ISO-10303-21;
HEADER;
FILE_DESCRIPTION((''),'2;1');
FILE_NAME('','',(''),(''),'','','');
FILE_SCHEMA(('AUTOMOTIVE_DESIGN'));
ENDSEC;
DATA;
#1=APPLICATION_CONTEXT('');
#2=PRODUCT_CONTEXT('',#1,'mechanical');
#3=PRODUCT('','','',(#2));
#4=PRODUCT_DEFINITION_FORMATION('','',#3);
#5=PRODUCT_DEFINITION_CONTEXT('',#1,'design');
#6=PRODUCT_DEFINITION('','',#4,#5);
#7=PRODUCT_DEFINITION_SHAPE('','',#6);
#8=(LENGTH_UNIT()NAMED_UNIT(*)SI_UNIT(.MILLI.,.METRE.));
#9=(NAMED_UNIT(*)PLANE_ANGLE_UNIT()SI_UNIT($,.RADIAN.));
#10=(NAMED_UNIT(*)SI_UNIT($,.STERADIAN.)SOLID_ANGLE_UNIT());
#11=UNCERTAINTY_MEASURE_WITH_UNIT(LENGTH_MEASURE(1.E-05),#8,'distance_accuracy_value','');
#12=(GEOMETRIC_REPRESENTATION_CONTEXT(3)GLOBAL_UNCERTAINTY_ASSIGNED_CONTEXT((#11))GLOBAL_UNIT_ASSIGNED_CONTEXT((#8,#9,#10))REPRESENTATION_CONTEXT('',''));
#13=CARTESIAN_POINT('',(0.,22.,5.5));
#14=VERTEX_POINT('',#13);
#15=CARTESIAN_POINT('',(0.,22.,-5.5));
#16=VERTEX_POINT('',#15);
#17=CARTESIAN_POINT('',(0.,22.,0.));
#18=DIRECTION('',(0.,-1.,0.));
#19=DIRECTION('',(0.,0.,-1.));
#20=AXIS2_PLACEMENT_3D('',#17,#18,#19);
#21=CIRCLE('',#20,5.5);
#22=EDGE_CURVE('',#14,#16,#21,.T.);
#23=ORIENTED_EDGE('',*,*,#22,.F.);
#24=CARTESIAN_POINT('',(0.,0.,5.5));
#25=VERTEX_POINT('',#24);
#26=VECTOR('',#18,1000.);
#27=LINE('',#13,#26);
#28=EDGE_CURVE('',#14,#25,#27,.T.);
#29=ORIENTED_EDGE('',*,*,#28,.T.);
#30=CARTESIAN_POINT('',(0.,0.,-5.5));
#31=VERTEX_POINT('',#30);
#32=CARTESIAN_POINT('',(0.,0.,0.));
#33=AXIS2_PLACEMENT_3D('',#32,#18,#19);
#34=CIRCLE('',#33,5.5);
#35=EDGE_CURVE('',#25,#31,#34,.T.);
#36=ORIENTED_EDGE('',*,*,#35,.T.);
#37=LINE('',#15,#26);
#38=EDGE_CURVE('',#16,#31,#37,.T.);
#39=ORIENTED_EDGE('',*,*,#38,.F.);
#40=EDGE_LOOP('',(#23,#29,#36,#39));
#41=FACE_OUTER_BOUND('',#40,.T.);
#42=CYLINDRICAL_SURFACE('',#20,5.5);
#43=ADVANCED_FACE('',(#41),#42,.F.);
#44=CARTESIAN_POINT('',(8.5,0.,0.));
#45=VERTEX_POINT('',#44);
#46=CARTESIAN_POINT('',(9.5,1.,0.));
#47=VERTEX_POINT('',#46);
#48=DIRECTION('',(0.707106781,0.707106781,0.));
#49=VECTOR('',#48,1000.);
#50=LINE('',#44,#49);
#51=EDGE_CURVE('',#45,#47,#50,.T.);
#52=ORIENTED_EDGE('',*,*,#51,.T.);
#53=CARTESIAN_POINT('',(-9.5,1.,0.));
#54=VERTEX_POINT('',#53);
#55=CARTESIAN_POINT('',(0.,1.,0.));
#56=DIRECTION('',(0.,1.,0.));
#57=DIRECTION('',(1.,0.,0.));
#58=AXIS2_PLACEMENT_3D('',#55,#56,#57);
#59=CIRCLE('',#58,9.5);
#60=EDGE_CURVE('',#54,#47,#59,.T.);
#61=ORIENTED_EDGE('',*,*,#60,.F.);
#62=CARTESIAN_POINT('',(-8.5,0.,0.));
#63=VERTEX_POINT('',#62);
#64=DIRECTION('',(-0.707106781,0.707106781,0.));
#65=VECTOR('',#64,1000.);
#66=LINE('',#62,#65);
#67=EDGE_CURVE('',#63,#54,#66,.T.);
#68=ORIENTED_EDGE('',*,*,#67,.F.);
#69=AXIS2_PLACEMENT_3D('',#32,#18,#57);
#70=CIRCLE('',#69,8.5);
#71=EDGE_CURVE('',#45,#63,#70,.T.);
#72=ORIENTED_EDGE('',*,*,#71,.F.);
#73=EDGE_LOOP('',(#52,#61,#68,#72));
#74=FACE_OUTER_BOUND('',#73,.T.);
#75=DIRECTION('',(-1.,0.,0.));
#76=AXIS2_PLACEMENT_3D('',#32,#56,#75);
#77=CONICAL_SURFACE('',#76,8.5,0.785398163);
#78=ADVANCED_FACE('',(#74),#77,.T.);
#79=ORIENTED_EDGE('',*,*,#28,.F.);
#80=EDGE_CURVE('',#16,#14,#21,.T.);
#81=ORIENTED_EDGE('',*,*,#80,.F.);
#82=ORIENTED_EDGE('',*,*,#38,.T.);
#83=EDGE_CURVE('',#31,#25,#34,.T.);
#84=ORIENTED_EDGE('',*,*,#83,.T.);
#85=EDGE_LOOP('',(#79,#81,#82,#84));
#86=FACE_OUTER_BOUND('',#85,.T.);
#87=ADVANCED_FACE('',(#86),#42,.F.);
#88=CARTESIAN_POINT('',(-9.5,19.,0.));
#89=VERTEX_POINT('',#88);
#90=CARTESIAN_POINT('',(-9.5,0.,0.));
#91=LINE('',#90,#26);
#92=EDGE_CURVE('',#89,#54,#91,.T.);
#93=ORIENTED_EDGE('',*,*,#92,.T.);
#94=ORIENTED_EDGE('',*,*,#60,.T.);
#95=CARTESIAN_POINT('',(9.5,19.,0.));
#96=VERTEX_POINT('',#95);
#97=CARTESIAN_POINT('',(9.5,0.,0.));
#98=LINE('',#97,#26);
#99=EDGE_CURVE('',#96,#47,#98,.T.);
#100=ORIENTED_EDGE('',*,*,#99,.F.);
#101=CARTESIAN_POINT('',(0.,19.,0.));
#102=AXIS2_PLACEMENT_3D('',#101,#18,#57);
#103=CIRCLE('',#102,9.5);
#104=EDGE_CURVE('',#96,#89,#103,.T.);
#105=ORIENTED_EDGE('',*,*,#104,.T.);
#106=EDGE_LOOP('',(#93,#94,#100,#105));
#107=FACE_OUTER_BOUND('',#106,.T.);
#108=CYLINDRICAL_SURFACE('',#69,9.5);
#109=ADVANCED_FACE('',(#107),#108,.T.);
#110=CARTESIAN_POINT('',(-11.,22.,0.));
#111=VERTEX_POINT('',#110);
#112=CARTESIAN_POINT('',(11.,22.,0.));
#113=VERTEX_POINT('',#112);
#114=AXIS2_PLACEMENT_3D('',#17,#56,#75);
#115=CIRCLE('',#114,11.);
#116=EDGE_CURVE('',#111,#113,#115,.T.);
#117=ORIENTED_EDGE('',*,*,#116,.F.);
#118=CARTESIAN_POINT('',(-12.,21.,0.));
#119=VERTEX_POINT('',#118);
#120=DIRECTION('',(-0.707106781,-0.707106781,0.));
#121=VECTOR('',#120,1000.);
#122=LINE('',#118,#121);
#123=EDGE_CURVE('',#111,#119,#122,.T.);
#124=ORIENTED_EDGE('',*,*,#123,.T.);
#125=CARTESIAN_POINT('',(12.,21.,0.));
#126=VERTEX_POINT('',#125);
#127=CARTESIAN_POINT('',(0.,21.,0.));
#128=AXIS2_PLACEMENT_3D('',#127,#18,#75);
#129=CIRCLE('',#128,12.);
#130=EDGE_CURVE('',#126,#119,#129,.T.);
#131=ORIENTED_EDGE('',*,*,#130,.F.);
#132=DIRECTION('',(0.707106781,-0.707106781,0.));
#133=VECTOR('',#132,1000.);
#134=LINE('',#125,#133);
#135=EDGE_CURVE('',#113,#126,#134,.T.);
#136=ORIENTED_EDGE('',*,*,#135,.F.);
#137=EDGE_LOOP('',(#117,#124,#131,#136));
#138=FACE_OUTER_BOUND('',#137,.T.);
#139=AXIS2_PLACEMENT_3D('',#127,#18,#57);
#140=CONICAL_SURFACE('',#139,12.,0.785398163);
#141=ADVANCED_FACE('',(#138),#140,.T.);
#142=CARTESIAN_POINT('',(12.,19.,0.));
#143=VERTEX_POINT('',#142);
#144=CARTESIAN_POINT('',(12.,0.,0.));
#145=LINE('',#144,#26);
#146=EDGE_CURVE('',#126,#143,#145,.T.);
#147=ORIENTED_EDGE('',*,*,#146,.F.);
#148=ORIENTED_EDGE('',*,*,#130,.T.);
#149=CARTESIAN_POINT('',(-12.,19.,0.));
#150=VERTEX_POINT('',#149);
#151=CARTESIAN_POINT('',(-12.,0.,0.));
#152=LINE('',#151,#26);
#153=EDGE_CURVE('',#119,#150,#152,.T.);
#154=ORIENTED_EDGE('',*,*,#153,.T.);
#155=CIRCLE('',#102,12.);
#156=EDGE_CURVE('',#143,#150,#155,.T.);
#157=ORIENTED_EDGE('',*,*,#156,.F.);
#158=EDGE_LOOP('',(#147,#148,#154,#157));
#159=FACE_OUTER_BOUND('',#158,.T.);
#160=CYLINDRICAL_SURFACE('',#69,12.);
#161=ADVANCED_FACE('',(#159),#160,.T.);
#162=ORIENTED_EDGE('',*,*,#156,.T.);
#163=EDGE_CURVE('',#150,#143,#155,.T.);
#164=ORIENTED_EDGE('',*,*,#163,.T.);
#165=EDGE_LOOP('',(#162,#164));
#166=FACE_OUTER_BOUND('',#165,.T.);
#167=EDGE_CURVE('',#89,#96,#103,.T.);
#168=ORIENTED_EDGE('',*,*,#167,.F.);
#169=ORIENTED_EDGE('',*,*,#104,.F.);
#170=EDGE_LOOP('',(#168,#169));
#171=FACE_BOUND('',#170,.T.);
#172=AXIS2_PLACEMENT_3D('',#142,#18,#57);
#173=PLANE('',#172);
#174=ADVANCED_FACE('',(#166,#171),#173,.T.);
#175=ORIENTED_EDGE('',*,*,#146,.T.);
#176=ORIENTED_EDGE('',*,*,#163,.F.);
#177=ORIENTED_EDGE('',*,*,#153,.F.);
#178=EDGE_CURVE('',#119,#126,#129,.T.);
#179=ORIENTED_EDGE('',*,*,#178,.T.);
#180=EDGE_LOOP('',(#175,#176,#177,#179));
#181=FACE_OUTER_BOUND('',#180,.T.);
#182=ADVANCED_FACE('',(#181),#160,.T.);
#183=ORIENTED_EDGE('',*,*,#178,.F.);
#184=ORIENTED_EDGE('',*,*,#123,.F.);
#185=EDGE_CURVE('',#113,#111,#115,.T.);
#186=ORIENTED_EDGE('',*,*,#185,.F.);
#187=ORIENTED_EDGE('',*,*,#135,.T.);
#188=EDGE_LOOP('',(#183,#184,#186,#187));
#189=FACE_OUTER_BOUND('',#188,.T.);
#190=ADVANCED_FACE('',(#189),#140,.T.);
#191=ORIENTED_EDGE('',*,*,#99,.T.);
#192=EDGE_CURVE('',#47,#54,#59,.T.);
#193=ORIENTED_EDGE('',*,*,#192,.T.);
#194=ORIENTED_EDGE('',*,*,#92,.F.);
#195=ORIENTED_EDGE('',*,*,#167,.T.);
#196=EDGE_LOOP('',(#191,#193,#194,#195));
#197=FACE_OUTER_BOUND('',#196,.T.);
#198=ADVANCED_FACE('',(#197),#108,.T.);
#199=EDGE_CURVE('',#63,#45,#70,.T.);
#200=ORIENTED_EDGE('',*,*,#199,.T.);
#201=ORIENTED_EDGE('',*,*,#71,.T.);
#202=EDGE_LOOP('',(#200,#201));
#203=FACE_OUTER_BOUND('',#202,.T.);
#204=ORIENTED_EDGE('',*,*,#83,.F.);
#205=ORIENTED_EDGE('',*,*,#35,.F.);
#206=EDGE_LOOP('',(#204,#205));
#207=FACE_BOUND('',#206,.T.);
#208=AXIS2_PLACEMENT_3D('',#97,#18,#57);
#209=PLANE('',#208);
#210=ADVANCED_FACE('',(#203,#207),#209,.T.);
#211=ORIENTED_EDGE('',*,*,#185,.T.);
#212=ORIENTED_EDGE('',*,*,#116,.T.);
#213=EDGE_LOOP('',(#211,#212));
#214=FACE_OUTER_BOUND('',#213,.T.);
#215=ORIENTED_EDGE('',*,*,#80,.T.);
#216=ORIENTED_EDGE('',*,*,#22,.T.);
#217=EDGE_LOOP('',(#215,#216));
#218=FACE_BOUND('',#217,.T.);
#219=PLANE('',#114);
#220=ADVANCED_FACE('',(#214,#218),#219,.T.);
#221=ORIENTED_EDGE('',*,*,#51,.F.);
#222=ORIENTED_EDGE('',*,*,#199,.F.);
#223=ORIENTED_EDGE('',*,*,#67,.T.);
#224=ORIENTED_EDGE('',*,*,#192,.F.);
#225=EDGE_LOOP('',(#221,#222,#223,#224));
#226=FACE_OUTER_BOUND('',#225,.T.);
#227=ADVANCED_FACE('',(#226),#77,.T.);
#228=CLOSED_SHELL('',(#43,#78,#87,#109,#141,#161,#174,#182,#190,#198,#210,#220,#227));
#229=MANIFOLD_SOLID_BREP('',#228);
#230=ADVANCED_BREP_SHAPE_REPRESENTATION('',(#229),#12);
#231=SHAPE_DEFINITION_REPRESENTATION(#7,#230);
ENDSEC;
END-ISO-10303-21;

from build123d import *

# Parameters (mm, degrees)
CUT_EXTRUDE_1_DEPTH      = 28.784887979
CUT_EXTRUDE_1_DEPTH_BACK = 28.784887979
SKETCH_2_R               = 5.5
CHAMFER_1_SIZE           = 1
CHAMFER_2_SIZE           = 1


with BuildPart() as part:
    # 草图1 → 旋转1 (revolve)
    with BuildSketch(Plane.XY):
        Polygon((0, 0), (0, 22), (12, 22), (12, 19), (9.5, 19), (9.5, 0), align=None)
    revolve(axis=Axis((0, 0, 0), (0, 1, 0)))

    # 草图2 → 切除-拉伸1 (cut, two sides: drawn at the far end of the back side and taken through both)
    with BuildSketch(Plane.XZ.offset(-CUT_EXTRUDE_1_DEPTH_BACK)):
        with Locations(Location((0, 0, 0), (0, 0, 270))):
            Circle(SKETCH_2_R)
    extrude(amount=CUT_EXTRUDE_1_DEPTH + CUT_EXTRUDE_1_DEPTH_BACK, mode=Mode.SUBTRACT)

    # 倒角1
    chamfer_1_edges = [part.edges().sort_by_distance(p)[0] for p in [
        (-12, 22, 0),
    ]]
    chamfer(chamfer_1_edges, length=CHAMFER_1_SIZE)

    # 倒角2
    chamfer_2_edges = [part.edges().sort_by_distance(p)[0] for p in [
        (-9.5, 0, 0),
    ]]
    chamfer(chamfer_2_edges, length=CHAMFER_2_SIZE)


solid = part.part
